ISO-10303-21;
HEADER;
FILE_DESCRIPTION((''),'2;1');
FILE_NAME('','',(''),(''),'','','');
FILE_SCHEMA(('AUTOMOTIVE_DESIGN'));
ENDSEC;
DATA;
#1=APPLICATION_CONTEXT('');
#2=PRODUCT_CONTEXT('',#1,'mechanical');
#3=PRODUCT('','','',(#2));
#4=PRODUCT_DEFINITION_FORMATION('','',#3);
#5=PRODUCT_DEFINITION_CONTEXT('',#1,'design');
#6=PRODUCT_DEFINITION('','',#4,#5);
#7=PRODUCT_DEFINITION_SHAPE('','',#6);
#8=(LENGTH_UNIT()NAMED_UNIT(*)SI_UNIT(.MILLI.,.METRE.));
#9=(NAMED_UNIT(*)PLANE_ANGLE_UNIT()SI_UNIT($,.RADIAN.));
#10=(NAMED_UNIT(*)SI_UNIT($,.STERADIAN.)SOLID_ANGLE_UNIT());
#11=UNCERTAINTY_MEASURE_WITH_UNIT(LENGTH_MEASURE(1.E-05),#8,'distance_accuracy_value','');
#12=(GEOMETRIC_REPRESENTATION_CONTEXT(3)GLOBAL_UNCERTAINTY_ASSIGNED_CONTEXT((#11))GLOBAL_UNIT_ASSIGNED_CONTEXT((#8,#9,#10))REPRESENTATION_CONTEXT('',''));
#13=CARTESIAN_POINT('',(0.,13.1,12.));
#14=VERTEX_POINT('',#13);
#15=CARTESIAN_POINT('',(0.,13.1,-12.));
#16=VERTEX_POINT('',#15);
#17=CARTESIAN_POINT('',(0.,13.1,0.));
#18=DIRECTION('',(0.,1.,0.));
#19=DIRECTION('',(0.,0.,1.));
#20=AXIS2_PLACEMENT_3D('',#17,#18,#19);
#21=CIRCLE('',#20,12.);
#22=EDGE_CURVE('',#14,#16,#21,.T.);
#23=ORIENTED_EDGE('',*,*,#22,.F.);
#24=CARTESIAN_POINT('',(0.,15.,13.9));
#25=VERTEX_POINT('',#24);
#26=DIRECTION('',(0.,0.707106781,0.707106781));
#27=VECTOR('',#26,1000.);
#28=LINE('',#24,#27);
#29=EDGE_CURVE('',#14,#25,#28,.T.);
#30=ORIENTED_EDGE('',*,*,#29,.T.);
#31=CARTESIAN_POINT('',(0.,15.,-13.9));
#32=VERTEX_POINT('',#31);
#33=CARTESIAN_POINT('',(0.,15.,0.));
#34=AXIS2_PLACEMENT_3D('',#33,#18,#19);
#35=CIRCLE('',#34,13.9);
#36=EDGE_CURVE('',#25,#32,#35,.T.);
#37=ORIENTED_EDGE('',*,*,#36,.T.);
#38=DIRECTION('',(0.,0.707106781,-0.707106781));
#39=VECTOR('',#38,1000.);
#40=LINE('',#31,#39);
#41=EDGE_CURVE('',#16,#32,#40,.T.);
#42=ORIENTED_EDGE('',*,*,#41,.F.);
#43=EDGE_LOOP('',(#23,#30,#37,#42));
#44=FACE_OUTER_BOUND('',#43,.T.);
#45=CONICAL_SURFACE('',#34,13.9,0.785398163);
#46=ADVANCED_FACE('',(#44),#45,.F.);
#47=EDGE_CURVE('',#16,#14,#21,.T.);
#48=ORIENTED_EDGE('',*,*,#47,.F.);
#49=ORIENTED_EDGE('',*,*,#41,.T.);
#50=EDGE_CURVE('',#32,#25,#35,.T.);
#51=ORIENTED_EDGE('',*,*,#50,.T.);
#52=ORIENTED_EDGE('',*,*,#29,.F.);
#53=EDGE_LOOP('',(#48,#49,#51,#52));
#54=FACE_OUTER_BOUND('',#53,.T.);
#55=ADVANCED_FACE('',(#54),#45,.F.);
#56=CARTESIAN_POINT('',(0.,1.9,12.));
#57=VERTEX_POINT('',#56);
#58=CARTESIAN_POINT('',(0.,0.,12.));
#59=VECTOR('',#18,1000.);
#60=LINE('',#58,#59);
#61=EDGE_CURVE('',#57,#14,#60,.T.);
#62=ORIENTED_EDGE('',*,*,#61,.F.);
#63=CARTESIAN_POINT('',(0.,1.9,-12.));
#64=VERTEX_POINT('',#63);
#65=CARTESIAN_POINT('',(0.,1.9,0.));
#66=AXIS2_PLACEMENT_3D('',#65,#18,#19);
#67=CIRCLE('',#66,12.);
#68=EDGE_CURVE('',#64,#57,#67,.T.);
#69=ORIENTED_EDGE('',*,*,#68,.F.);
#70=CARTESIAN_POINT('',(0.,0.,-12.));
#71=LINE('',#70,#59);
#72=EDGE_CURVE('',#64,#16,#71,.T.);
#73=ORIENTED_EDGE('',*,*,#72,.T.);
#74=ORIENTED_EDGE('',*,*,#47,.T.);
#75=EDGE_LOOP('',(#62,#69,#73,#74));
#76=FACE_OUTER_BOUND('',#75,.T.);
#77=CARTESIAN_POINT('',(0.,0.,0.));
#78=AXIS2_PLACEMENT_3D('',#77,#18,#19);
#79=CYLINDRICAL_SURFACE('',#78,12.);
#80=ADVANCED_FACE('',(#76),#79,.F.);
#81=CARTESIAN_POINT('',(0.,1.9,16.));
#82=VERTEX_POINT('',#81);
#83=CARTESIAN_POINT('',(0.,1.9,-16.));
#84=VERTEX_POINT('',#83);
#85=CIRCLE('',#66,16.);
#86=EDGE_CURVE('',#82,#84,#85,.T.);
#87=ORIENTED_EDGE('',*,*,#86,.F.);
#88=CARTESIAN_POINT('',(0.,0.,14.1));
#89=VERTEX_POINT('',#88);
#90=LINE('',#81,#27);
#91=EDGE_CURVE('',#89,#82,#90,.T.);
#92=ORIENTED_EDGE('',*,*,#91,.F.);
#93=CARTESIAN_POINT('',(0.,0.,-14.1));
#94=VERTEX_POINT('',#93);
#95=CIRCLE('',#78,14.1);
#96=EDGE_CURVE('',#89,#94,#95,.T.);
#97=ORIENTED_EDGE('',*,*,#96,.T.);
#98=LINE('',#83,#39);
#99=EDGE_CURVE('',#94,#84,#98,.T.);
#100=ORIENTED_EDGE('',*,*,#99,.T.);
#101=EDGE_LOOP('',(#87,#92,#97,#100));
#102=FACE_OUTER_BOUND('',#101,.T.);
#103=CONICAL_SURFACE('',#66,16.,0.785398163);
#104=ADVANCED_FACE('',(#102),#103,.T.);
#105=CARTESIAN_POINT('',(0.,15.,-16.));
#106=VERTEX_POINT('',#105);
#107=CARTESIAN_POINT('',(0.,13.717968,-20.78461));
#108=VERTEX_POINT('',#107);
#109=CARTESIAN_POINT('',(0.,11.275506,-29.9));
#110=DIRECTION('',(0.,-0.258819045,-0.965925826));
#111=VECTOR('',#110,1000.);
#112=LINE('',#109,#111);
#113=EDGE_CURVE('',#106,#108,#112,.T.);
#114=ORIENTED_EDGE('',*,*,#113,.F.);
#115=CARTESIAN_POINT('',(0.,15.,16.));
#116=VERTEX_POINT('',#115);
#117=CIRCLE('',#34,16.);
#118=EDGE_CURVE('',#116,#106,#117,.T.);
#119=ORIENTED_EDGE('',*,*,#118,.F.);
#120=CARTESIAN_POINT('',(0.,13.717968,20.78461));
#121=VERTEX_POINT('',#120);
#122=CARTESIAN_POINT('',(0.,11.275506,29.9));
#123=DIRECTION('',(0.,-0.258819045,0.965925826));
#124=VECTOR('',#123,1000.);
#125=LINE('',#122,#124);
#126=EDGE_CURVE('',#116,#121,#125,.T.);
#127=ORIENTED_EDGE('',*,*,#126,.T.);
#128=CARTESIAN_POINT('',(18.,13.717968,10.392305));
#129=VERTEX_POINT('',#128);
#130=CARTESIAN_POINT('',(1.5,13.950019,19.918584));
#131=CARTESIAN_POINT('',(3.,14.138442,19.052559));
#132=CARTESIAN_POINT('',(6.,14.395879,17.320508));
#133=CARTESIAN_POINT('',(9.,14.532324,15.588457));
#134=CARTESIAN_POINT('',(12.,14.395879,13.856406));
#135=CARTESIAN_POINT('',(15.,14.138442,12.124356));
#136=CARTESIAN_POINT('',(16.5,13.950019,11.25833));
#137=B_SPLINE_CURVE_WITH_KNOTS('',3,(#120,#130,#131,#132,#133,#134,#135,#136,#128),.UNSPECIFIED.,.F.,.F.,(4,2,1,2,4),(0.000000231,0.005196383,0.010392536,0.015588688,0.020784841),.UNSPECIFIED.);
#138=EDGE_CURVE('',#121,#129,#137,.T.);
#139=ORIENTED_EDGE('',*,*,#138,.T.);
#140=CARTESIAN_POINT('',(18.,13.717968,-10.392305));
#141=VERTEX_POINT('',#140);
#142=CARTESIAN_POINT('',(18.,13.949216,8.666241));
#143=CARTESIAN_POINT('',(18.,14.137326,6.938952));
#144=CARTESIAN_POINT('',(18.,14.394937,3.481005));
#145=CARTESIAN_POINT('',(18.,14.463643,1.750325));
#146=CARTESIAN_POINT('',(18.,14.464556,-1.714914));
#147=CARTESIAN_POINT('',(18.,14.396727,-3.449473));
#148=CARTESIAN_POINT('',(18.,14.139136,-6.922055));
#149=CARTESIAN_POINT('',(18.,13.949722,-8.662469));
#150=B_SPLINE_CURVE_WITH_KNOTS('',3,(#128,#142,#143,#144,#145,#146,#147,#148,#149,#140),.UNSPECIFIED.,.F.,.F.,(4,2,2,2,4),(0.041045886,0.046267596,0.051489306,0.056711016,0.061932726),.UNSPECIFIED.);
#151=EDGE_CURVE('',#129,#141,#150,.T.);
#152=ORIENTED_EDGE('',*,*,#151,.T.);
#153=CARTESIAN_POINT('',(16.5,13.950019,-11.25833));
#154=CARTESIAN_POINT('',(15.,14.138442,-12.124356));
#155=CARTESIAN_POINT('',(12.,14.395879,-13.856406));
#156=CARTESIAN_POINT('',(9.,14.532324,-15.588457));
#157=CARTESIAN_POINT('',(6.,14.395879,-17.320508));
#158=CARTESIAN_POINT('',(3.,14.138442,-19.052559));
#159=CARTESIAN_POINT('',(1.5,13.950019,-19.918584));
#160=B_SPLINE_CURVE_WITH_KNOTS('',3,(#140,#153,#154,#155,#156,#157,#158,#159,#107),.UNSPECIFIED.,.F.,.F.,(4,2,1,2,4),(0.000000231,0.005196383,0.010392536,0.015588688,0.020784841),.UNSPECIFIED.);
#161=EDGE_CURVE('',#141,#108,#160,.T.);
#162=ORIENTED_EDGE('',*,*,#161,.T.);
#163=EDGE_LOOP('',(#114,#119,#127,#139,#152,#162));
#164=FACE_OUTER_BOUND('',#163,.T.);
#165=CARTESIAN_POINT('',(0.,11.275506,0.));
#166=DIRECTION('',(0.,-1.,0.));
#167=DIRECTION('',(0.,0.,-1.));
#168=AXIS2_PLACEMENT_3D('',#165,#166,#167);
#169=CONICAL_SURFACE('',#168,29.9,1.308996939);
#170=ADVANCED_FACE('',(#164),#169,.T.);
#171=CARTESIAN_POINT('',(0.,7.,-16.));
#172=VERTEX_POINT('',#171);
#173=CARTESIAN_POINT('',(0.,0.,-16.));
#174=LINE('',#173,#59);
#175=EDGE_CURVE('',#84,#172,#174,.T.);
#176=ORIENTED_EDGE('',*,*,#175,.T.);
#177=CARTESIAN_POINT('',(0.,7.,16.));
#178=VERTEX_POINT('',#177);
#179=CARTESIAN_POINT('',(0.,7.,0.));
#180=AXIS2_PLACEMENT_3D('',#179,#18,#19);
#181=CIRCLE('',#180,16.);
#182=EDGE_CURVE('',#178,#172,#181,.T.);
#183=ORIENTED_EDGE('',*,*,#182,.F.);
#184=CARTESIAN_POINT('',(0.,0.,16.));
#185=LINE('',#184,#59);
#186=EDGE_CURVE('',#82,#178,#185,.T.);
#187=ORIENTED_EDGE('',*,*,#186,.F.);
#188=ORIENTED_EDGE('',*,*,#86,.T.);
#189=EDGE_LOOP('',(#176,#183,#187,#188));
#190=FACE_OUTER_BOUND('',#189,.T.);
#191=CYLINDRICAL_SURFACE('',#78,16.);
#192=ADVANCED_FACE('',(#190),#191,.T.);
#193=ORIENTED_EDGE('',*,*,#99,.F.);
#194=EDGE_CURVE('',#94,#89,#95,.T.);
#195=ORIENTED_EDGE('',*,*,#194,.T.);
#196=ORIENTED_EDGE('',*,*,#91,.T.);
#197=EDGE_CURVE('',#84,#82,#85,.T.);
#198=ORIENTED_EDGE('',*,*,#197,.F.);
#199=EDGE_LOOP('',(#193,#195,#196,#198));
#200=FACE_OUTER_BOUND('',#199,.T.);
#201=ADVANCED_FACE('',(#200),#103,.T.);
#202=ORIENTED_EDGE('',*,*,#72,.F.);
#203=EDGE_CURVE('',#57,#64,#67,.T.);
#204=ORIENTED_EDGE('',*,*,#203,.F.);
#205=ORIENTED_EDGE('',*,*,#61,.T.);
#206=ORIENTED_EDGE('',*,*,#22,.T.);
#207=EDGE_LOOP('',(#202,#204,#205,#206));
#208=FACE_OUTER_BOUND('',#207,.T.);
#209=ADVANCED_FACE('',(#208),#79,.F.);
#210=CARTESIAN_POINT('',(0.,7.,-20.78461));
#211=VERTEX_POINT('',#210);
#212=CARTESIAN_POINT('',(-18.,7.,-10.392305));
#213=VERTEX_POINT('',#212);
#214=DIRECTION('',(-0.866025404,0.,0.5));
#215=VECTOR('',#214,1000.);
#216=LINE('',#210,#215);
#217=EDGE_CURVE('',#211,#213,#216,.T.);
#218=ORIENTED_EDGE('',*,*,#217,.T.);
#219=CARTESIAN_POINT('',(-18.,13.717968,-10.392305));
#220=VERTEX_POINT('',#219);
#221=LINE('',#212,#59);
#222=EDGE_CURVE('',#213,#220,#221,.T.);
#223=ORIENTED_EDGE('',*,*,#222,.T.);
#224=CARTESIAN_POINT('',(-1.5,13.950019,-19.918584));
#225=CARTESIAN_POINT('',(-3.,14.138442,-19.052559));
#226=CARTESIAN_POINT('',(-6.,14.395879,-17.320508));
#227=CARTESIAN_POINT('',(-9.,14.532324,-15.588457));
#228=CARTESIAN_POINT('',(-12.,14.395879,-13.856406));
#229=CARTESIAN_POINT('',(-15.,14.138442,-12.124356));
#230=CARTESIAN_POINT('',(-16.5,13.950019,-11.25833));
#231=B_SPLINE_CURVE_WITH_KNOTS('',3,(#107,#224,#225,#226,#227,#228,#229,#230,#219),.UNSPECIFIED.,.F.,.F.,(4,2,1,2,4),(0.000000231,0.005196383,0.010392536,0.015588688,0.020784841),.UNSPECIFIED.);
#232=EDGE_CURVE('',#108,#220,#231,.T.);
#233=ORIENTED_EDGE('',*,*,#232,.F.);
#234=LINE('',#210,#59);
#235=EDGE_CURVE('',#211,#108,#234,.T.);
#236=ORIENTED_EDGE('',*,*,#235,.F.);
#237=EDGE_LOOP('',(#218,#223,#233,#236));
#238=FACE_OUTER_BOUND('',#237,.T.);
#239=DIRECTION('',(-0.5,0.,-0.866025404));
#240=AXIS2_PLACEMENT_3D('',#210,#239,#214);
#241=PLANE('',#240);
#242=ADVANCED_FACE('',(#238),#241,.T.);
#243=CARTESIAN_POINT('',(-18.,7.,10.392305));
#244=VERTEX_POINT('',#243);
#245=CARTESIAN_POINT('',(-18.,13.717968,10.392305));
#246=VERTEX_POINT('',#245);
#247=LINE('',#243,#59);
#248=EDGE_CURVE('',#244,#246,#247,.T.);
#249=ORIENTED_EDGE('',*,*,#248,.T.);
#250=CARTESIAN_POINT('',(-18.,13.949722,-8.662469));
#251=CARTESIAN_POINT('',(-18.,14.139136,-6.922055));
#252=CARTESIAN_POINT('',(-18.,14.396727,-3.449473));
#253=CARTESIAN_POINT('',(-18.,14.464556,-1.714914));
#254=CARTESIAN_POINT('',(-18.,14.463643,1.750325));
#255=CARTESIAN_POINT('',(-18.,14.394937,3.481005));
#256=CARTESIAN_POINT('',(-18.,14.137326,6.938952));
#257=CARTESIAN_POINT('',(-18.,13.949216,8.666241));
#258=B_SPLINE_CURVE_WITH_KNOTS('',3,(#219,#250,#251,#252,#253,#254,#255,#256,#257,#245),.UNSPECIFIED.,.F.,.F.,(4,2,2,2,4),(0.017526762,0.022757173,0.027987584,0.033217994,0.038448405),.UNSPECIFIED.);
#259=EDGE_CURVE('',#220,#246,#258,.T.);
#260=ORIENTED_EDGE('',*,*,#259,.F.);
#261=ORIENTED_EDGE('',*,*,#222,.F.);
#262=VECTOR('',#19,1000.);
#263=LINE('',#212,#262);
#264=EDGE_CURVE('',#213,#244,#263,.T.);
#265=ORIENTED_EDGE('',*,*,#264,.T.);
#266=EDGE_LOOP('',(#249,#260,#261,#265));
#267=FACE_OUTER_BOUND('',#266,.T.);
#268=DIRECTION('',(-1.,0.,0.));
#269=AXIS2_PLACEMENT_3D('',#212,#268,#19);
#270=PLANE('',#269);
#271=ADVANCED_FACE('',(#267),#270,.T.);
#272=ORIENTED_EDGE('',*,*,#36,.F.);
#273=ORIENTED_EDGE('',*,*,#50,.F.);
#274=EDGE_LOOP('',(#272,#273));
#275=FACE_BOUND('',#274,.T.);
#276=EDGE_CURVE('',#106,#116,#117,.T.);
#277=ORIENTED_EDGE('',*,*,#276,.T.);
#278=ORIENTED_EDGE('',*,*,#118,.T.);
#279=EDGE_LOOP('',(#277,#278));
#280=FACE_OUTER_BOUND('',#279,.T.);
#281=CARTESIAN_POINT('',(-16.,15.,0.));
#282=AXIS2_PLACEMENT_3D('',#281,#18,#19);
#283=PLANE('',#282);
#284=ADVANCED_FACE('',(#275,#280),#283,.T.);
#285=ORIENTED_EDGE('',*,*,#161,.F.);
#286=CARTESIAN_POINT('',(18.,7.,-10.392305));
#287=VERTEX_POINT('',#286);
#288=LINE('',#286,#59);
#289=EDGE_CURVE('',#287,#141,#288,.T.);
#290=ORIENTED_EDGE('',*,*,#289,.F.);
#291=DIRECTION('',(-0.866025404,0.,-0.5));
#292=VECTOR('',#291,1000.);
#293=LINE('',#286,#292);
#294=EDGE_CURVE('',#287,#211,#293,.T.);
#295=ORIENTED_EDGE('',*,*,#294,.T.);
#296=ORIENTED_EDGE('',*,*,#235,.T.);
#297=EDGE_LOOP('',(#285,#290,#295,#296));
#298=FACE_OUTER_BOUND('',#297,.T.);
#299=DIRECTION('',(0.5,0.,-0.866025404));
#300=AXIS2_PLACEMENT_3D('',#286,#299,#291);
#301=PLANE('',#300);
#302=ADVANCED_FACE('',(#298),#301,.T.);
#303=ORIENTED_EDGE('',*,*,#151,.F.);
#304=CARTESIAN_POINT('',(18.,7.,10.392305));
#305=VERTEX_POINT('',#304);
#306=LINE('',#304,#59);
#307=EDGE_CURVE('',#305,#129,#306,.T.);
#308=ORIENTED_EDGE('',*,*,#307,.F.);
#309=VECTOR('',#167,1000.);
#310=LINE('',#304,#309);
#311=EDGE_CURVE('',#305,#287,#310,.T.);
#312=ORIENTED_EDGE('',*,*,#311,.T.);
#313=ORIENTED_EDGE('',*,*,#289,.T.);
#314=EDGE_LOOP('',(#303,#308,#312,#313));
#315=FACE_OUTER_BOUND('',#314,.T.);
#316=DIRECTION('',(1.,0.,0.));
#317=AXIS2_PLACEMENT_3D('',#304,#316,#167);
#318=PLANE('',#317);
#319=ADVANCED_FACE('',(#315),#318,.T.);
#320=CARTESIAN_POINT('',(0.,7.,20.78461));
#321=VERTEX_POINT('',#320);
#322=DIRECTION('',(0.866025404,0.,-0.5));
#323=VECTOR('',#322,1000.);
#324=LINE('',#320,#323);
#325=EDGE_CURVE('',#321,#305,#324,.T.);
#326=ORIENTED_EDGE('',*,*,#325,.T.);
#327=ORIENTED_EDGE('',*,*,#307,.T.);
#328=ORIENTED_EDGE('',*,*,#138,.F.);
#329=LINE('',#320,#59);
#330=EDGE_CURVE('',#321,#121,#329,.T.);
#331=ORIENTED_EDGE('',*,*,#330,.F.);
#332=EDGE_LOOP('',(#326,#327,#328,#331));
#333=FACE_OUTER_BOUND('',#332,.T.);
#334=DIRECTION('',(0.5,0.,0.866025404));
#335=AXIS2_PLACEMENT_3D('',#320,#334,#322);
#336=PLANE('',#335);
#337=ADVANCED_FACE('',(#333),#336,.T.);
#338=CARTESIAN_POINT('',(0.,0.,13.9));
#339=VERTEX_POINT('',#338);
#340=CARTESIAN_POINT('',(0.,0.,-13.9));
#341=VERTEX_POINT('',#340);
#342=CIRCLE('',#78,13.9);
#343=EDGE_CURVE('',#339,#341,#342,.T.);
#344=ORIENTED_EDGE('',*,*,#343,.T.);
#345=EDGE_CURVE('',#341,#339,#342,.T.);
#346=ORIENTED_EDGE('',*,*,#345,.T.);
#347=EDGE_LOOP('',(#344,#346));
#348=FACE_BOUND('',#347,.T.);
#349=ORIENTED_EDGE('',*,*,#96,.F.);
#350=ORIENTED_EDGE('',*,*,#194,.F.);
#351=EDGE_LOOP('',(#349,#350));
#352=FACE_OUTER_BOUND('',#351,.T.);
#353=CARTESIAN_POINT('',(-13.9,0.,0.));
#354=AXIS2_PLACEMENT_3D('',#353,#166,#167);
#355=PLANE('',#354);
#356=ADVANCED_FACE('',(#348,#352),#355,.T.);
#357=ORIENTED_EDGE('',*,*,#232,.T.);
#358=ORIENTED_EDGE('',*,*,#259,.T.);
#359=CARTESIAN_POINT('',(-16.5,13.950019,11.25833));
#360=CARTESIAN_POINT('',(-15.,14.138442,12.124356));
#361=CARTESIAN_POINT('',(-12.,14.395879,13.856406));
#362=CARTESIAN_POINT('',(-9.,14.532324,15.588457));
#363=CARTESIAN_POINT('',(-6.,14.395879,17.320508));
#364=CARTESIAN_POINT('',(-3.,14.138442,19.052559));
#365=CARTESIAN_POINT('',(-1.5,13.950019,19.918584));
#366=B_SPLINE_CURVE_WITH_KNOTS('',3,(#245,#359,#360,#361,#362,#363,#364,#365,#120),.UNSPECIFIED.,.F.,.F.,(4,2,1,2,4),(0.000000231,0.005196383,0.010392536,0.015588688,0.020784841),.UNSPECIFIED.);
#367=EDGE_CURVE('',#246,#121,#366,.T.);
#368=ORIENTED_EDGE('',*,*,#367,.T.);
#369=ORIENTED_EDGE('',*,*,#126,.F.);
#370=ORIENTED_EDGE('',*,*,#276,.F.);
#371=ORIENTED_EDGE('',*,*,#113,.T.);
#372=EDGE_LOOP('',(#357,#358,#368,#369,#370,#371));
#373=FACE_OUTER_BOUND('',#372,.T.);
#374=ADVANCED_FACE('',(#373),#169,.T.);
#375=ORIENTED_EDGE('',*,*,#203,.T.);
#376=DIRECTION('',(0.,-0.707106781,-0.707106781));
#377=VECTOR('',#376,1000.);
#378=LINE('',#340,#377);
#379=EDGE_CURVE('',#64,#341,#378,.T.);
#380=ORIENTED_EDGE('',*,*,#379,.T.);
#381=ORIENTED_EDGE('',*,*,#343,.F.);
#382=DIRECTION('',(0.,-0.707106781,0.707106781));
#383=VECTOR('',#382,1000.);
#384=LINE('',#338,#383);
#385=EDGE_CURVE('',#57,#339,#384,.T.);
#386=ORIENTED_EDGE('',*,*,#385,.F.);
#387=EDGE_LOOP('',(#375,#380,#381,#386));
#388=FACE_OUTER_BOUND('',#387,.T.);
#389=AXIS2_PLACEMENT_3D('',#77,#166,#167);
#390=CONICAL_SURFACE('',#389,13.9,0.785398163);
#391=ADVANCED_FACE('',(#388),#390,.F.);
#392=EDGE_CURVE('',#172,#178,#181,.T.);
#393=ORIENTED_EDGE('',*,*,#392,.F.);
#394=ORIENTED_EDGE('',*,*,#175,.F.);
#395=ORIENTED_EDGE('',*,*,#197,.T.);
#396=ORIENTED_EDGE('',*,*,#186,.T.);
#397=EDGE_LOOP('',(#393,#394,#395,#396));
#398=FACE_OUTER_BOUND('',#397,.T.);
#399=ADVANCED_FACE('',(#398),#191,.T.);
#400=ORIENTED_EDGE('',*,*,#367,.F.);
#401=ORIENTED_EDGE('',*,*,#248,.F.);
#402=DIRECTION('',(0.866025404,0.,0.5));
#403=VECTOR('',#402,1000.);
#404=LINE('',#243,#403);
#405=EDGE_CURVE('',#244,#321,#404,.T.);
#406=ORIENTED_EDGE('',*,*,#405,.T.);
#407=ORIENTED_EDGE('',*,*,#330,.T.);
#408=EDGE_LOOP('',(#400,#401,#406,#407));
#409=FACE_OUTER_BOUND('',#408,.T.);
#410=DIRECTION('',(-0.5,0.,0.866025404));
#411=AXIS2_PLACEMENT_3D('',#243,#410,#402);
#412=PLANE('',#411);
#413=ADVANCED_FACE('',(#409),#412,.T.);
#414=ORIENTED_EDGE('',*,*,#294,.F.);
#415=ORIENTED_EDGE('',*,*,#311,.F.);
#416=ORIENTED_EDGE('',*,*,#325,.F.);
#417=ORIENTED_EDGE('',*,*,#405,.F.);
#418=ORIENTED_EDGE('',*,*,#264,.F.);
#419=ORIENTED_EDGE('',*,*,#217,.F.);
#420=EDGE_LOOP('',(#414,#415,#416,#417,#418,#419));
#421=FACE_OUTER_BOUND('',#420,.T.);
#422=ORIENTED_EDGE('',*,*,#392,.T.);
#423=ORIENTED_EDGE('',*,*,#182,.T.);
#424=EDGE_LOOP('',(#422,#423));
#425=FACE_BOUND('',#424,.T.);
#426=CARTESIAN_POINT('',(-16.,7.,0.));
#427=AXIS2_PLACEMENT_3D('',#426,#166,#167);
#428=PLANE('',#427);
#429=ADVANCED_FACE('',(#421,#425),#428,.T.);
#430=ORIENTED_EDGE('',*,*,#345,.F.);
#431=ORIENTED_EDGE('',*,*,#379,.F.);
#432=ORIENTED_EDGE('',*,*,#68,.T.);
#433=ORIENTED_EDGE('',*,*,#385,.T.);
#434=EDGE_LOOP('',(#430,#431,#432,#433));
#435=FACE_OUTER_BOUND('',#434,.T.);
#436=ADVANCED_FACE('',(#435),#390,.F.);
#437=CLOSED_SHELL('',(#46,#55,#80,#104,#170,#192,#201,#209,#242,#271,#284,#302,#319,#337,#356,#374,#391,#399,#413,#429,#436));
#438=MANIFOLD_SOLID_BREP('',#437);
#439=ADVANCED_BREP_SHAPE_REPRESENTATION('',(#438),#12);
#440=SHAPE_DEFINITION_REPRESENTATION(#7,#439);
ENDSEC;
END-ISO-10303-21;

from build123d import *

# Parameters (mm, degrees)
EXTRUDE_1_DEPTH = 8


with BuildPart() as part:
    # 草图1 → 旋转1 (revolve)
    with BuildSketch(Plane.XY, mode=Mode.PRIVATE) as revolve_1_sk:
        Polygon((-13.9, 0), (-14.1, 0), (-16, 1.9), (-16, 7), (-18, 7), (-18, 14.464101615), (-16, 15), (-13.9, 15), (-12, 13.1), (-12, 1.9), align=None)
    revolve(revolve_1_sk.sketch.rotate(Axis((0, 0, 0), (0, -1, 0)), 270), axis=Axis((0, 0, 0), (0, -1, 0)))

    # 草图2 → 拉伸1 (add)
    with BuildSketch(Plane(origin=(0, 15, 0), x_dir=(1, 0, 0), z_dir=(0, 1, 0))):
        Polygon((18, -10.392304845), (18, 10.392304845), (0, 20.784609691), (-18, 10.392304845), (-18, -10.392304845), (0, -20.784609691), align=None)
    extrude(amount=-EXTRUDE_1_DEPTH)

    # 草图3 → 切除-旋转2 (revolve, cut)
    with BuildSketch(Plane.XY, mode=Mode.PRIVATE) as cut_revolve_2_sk:
        Polygon((-29.9, 11.275506225), (-16, 15), (-29.9, 15), align=None)
        Polygon((-13.9, 15), (-12, 13.1), (-12, 0), (0, 0), (0, 15), align=None)
    revolve(cut_revolve_2_sk.sketch.rotate(Axis((0, 0, 0), (0, -1, 0)), 270), axis=Axis((0, 0, 0), (0, -1, 0)), mode=Mode.SUBTRACT)


solid = part.part
